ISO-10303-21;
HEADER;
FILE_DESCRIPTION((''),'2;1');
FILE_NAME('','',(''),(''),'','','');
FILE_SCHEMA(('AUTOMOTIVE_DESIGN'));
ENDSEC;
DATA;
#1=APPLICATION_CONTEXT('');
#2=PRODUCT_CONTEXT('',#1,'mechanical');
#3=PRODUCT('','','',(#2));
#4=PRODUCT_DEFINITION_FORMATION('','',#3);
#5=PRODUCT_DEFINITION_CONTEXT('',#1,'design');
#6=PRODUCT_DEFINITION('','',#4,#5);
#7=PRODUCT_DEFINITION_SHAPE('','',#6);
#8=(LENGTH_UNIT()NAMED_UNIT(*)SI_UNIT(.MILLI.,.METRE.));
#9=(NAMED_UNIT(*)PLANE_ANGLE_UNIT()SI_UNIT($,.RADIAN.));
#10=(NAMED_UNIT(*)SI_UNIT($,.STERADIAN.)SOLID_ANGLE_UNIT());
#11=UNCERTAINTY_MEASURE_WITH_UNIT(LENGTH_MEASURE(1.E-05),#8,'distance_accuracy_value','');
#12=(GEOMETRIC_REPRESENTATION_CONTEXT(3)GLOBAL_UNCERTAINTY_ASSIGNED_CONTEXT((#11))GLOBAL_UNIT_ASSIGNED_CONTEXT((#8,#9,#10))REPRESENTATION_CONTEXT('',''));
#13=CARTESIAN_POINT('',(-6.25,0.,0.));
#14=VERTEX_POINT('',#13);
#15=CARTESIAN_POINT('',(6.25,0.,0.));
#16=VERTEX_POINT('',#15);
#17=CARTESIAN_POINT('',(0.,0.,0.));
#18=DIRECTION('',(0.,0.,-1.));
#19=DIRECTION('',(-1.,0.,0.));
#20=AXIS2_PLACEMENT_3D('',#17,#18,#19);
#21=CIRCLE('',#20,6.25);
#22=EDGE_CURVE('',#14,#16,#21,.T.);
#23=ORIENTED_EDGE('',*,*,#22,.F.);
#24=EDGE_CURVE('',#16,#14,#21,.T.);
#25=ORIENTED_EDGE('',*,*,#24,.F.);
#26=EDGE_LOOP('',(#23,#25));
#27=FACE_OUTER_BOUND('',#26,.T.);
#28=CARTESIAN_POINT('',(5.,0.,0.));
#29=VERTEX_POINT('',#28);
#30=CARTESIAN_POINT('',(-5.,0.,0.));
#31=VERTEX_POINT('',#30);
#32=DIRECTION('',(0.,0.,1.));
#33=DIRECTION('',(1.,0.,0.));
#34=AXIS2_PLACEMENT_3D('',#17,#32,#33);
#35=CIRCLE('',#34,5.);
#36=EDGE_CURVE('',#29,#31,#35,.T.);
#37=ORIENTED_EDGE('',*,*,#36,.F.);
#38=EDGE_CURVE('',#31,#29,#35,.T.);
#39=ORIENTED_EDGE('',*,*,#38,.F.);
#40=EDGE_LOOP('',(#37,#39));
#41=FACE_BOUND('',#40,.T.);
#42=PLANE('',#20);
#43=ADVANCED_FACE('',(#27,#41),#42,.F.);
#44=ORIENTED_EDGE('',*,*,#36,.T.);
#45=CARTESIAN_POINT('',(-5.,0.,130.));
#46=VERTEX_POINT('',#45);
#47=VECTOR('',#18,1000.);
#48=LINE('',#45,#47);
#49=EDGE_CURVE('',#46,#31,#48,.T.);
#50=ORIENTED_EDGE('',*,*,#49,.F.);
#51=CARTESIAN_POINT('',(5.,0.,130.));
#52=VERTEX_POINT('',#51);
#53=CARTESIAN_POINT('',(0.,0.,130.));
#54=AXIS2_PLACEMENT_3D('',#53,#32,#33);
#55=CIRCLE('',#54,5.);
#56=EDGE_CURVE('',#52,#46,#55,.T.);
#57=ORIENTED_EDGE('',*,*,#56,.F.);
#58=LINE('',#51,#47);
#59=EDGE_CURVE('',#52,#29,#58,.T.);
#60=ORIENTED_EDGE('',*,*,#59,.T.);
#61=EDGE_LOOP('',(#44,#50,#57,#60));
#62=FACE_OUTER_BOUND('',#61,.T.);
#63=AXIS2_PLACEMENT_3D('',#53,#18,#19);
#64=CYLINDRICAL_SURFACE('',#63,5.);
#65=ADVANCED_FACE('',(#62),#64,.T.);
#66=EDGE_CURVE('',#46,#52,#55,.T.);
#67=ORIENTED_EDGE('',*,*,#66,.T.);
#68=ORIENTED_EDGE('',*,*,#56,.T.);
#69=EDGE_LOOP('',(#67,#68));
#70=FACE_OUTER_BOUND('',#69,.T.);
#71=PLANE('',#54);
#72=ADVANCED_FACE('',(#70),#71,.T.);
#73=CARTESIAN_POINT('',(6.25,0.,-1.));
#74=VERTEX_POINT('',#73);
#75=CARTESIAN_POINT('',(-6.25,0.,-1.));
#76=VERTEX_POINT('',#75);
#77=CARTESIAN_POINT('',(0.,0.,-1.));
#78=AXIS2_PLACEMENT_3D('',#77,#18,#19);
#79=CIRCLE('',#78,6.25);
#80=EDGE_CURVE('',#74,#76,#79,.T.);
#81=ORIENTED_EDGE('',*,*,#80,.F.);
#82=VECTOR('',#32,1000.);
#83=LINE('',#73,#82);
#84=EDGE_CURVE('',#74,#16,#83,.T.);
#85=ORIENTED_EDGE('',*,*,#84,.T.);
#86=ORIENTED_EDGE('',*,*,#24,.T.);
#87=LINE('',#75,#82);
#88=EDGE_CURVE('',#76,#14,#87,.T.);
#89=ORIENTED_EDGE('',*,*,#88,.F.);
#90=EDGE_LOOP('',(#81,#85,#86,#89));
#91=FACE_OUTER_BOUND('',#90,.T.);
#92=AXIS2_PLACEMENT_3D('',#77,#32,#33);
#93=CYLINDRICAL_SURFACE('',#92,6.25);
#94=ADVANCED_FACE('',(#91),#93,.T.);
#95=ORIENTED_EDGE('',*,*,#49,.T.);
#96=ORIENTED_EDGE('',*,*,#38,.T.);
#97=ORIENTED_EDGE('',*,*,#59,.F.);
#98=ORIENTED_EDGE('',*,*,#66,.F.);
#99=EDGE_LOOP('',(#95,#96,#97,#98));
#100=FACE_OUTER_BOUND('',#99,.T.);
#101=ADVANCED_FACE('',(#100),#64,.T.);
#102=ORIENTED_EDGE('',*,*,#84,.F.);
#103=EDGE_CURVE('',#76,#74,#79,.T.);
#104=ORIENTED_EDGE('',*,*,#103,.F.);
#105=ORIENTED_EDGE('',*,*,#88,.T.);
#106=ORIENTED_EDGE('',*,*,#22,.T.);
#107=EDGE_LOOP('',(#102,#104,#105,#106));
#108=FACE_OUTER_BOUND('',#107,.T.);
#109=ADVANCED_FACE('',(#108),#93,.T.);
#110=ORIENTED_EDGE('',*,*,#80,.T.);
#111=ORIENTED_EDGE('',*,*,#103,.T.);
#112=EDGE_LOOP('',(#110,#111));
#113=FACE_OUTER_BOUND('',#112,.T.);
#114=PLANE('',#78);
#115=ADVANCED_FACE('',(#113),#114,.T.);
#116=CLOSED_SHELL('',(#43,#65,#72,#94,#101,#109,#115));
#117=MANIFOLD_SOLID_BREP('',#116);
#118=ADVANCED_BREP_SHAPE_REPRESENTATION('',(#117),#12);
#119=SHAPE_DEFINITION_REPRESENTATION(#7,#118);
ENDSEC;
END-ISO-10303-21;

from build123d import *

# Parameters (mm, degrees)
SKETCH_1_R      = 5
EXTRUDE_1_DEPTH = 130
SKETCH_2_R      = 6.25
EXTRUDE_2_DEPTH = 1


with BuildPart() as part:
    # 草图1 → 凸台-拉伸1 (new body)
    with BuildSketch(Plane.XY):
        Circle(SKETCH_1_R)
    extrude(amount=EXTRUDE_1_DEPTH)

    # 草图2 → 凸台-拉伸2 (add)
    with BuildSketch(Plane(origin=(0, 0, 0), x_dir=(-1, 0, 0), z_dir=(0, 0, -1))):
        Circle(SKETCH_2_R)
    extrude(amount=EXTRUDE_2_DEPTH)


solid = part.part
